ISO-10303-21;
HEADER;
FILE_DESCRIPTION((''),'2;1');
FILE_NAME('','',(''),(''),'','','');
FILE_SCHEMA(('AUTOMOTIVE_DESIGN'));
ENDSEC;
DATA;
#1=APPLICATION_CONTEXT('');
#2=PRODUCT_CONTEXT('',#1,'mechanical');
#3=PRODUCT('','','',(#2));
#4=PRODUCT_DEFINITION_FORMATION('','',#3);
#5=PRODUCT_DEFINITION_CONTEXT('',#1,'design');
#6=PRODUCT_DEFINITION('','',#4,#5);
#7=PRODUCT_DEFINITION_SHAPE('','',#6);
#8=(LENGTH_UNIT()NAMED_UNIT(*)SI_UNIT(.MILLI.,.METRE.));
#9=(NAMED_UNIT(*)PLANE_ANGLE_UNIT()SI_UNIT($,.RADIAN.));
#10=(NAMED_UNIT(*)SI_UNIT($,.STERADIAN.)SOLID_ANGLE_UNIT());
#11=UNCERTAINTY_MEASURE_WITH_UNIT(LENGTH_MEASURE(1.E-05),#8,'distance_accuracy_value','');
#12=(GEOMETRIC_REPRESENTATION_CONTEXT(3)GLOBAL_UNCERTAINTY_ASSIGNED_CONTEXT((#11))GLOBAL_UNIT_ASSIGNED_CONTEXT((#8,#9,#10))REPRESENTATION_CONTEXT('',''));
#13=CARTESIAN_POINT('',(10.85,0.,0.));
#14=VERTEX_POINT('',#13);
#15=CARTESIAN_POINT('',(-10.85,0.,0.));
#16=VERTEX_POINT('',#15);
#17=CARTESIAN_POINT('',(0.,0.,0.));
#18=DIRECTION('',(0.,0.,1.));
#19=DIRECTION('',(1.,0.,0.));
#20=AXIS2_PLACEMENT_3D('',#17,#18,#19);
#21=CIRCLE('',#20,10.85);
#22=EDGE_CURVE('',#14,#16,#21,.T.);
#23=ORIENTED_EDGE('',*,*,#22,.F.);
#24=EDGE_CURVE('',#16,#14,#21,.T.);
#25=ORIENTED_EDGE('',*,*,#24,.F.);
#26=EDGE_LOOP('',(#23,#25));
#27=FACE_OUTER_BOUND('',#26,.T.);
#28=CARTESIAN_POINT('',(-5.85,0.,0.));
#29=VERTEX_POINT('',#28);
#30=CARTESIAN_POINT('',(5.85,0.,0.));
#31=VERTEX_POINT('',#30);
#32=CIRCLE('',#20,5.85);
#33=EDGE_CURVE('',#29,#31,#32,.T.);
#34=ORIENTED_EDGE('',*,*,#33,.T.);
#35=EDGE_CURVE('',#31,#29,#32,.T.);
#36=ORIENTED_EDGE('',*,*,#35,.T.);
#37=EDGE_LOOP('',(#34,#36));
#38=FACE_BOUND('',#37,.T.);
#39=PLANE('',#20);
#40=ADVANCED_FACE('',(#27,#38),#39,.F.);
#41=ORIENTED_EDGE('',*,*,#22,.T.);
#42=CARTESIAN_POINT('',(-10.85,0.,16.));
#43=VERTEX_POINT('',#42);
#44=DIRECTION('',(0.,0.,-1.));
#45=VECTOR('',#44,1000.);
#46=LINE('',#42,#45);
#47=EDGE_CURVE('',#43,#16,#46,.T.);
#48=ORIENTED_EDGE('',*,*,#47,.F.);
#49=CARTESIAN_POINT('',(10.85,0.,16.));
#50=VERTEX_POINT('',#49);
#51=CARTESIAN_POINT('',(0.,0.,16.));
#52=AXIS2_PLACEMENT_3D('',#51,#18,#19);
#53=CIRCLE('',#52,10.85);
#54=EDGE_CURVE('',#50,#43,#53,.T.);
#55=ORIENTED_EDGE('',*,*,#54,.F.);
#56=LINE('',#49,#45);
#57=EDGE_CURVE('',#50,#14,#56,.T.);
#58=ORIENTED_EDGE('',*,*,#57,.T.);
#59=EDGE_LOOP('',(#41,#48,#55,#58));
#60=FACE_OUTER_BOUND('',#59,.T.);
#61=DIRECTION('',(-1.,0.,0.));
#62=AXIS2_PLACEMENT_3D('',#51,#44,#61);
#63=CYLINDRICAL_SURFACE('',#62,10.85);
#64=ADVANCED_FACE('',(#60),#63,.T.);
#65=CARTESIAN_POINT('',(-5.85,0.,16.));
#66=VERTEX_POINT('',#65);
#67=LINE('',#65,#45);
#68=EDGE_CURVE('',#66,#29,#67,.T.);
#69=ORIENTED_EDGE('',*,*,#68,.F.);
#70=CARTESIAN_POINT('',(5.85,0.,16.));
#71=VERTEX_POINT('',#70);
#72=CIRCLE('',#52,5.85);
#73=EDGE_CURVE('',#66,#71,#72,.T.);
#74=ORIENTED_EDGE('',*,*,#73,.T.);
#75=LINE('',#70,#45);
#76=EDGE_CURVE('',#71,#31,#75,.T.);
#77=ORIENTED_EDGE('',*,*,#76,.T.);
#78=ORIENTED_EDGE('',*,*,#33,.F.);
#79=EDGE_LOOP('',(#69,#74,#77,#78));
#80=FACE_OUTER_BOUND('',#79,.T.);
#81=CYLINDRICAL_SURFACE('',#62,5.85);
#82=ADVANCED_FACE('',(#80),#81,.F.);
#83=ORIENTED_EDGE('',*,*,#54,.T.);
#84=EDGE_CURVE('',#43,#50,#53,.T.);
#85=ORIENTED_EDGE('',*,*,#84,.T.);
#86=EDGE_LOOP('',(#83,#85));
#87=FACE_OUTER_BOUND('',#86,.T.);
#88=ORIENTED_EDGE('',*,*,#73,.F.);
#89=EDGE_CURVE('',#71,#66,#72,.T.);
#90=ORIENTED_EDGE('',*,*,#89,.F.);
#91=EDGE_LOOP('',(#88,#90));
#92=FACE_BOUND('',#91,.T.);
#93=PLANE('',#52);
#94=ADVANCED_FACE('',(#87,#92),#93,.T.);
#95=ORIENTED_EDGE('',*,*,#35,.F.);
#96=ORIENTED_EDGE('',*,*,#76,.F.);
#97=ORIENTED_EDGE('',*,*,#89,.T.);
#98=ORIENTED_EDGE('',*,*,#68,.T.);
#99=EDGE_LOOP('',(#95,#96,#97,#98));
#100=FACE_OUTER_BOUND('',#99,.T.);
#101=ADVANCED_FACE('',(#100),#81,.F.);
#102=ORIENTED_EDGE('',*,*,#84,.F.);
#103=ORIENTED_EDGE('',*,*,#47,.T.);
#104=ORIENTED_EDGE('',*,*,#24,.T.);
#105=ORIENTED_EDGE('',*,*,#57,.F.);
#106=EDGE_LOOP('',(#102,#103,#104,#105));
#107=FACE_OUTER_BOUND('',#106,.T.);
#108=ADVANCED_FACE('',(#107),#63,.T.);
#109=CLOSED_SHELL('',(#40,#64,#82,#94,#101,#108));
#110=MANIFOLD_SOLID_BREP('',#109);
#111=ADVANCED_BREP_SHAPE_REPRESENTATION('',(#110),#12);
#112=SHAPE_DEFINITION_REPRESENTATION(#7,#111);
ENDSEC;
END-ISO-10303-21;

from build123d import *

# Parameters (mm, degrees)
SKETCH1_R           = 10.85
SKETCH1_R_2         = 5.85
BOSS_EXTRUDE1_DEPTH = 16


with BuildPart() as part:
    # Sketch1 → Boss-Extrude1 (new body)
    with BuildSketch(Plane.XY):
        Circle(SKETCH1_R)
        Circle(SKETCH1_R_2, mode=Mode.SUBTRACT)
    extrude(amount=BOSS_EXTRUDE1_DEPTH)


solid = part.part
